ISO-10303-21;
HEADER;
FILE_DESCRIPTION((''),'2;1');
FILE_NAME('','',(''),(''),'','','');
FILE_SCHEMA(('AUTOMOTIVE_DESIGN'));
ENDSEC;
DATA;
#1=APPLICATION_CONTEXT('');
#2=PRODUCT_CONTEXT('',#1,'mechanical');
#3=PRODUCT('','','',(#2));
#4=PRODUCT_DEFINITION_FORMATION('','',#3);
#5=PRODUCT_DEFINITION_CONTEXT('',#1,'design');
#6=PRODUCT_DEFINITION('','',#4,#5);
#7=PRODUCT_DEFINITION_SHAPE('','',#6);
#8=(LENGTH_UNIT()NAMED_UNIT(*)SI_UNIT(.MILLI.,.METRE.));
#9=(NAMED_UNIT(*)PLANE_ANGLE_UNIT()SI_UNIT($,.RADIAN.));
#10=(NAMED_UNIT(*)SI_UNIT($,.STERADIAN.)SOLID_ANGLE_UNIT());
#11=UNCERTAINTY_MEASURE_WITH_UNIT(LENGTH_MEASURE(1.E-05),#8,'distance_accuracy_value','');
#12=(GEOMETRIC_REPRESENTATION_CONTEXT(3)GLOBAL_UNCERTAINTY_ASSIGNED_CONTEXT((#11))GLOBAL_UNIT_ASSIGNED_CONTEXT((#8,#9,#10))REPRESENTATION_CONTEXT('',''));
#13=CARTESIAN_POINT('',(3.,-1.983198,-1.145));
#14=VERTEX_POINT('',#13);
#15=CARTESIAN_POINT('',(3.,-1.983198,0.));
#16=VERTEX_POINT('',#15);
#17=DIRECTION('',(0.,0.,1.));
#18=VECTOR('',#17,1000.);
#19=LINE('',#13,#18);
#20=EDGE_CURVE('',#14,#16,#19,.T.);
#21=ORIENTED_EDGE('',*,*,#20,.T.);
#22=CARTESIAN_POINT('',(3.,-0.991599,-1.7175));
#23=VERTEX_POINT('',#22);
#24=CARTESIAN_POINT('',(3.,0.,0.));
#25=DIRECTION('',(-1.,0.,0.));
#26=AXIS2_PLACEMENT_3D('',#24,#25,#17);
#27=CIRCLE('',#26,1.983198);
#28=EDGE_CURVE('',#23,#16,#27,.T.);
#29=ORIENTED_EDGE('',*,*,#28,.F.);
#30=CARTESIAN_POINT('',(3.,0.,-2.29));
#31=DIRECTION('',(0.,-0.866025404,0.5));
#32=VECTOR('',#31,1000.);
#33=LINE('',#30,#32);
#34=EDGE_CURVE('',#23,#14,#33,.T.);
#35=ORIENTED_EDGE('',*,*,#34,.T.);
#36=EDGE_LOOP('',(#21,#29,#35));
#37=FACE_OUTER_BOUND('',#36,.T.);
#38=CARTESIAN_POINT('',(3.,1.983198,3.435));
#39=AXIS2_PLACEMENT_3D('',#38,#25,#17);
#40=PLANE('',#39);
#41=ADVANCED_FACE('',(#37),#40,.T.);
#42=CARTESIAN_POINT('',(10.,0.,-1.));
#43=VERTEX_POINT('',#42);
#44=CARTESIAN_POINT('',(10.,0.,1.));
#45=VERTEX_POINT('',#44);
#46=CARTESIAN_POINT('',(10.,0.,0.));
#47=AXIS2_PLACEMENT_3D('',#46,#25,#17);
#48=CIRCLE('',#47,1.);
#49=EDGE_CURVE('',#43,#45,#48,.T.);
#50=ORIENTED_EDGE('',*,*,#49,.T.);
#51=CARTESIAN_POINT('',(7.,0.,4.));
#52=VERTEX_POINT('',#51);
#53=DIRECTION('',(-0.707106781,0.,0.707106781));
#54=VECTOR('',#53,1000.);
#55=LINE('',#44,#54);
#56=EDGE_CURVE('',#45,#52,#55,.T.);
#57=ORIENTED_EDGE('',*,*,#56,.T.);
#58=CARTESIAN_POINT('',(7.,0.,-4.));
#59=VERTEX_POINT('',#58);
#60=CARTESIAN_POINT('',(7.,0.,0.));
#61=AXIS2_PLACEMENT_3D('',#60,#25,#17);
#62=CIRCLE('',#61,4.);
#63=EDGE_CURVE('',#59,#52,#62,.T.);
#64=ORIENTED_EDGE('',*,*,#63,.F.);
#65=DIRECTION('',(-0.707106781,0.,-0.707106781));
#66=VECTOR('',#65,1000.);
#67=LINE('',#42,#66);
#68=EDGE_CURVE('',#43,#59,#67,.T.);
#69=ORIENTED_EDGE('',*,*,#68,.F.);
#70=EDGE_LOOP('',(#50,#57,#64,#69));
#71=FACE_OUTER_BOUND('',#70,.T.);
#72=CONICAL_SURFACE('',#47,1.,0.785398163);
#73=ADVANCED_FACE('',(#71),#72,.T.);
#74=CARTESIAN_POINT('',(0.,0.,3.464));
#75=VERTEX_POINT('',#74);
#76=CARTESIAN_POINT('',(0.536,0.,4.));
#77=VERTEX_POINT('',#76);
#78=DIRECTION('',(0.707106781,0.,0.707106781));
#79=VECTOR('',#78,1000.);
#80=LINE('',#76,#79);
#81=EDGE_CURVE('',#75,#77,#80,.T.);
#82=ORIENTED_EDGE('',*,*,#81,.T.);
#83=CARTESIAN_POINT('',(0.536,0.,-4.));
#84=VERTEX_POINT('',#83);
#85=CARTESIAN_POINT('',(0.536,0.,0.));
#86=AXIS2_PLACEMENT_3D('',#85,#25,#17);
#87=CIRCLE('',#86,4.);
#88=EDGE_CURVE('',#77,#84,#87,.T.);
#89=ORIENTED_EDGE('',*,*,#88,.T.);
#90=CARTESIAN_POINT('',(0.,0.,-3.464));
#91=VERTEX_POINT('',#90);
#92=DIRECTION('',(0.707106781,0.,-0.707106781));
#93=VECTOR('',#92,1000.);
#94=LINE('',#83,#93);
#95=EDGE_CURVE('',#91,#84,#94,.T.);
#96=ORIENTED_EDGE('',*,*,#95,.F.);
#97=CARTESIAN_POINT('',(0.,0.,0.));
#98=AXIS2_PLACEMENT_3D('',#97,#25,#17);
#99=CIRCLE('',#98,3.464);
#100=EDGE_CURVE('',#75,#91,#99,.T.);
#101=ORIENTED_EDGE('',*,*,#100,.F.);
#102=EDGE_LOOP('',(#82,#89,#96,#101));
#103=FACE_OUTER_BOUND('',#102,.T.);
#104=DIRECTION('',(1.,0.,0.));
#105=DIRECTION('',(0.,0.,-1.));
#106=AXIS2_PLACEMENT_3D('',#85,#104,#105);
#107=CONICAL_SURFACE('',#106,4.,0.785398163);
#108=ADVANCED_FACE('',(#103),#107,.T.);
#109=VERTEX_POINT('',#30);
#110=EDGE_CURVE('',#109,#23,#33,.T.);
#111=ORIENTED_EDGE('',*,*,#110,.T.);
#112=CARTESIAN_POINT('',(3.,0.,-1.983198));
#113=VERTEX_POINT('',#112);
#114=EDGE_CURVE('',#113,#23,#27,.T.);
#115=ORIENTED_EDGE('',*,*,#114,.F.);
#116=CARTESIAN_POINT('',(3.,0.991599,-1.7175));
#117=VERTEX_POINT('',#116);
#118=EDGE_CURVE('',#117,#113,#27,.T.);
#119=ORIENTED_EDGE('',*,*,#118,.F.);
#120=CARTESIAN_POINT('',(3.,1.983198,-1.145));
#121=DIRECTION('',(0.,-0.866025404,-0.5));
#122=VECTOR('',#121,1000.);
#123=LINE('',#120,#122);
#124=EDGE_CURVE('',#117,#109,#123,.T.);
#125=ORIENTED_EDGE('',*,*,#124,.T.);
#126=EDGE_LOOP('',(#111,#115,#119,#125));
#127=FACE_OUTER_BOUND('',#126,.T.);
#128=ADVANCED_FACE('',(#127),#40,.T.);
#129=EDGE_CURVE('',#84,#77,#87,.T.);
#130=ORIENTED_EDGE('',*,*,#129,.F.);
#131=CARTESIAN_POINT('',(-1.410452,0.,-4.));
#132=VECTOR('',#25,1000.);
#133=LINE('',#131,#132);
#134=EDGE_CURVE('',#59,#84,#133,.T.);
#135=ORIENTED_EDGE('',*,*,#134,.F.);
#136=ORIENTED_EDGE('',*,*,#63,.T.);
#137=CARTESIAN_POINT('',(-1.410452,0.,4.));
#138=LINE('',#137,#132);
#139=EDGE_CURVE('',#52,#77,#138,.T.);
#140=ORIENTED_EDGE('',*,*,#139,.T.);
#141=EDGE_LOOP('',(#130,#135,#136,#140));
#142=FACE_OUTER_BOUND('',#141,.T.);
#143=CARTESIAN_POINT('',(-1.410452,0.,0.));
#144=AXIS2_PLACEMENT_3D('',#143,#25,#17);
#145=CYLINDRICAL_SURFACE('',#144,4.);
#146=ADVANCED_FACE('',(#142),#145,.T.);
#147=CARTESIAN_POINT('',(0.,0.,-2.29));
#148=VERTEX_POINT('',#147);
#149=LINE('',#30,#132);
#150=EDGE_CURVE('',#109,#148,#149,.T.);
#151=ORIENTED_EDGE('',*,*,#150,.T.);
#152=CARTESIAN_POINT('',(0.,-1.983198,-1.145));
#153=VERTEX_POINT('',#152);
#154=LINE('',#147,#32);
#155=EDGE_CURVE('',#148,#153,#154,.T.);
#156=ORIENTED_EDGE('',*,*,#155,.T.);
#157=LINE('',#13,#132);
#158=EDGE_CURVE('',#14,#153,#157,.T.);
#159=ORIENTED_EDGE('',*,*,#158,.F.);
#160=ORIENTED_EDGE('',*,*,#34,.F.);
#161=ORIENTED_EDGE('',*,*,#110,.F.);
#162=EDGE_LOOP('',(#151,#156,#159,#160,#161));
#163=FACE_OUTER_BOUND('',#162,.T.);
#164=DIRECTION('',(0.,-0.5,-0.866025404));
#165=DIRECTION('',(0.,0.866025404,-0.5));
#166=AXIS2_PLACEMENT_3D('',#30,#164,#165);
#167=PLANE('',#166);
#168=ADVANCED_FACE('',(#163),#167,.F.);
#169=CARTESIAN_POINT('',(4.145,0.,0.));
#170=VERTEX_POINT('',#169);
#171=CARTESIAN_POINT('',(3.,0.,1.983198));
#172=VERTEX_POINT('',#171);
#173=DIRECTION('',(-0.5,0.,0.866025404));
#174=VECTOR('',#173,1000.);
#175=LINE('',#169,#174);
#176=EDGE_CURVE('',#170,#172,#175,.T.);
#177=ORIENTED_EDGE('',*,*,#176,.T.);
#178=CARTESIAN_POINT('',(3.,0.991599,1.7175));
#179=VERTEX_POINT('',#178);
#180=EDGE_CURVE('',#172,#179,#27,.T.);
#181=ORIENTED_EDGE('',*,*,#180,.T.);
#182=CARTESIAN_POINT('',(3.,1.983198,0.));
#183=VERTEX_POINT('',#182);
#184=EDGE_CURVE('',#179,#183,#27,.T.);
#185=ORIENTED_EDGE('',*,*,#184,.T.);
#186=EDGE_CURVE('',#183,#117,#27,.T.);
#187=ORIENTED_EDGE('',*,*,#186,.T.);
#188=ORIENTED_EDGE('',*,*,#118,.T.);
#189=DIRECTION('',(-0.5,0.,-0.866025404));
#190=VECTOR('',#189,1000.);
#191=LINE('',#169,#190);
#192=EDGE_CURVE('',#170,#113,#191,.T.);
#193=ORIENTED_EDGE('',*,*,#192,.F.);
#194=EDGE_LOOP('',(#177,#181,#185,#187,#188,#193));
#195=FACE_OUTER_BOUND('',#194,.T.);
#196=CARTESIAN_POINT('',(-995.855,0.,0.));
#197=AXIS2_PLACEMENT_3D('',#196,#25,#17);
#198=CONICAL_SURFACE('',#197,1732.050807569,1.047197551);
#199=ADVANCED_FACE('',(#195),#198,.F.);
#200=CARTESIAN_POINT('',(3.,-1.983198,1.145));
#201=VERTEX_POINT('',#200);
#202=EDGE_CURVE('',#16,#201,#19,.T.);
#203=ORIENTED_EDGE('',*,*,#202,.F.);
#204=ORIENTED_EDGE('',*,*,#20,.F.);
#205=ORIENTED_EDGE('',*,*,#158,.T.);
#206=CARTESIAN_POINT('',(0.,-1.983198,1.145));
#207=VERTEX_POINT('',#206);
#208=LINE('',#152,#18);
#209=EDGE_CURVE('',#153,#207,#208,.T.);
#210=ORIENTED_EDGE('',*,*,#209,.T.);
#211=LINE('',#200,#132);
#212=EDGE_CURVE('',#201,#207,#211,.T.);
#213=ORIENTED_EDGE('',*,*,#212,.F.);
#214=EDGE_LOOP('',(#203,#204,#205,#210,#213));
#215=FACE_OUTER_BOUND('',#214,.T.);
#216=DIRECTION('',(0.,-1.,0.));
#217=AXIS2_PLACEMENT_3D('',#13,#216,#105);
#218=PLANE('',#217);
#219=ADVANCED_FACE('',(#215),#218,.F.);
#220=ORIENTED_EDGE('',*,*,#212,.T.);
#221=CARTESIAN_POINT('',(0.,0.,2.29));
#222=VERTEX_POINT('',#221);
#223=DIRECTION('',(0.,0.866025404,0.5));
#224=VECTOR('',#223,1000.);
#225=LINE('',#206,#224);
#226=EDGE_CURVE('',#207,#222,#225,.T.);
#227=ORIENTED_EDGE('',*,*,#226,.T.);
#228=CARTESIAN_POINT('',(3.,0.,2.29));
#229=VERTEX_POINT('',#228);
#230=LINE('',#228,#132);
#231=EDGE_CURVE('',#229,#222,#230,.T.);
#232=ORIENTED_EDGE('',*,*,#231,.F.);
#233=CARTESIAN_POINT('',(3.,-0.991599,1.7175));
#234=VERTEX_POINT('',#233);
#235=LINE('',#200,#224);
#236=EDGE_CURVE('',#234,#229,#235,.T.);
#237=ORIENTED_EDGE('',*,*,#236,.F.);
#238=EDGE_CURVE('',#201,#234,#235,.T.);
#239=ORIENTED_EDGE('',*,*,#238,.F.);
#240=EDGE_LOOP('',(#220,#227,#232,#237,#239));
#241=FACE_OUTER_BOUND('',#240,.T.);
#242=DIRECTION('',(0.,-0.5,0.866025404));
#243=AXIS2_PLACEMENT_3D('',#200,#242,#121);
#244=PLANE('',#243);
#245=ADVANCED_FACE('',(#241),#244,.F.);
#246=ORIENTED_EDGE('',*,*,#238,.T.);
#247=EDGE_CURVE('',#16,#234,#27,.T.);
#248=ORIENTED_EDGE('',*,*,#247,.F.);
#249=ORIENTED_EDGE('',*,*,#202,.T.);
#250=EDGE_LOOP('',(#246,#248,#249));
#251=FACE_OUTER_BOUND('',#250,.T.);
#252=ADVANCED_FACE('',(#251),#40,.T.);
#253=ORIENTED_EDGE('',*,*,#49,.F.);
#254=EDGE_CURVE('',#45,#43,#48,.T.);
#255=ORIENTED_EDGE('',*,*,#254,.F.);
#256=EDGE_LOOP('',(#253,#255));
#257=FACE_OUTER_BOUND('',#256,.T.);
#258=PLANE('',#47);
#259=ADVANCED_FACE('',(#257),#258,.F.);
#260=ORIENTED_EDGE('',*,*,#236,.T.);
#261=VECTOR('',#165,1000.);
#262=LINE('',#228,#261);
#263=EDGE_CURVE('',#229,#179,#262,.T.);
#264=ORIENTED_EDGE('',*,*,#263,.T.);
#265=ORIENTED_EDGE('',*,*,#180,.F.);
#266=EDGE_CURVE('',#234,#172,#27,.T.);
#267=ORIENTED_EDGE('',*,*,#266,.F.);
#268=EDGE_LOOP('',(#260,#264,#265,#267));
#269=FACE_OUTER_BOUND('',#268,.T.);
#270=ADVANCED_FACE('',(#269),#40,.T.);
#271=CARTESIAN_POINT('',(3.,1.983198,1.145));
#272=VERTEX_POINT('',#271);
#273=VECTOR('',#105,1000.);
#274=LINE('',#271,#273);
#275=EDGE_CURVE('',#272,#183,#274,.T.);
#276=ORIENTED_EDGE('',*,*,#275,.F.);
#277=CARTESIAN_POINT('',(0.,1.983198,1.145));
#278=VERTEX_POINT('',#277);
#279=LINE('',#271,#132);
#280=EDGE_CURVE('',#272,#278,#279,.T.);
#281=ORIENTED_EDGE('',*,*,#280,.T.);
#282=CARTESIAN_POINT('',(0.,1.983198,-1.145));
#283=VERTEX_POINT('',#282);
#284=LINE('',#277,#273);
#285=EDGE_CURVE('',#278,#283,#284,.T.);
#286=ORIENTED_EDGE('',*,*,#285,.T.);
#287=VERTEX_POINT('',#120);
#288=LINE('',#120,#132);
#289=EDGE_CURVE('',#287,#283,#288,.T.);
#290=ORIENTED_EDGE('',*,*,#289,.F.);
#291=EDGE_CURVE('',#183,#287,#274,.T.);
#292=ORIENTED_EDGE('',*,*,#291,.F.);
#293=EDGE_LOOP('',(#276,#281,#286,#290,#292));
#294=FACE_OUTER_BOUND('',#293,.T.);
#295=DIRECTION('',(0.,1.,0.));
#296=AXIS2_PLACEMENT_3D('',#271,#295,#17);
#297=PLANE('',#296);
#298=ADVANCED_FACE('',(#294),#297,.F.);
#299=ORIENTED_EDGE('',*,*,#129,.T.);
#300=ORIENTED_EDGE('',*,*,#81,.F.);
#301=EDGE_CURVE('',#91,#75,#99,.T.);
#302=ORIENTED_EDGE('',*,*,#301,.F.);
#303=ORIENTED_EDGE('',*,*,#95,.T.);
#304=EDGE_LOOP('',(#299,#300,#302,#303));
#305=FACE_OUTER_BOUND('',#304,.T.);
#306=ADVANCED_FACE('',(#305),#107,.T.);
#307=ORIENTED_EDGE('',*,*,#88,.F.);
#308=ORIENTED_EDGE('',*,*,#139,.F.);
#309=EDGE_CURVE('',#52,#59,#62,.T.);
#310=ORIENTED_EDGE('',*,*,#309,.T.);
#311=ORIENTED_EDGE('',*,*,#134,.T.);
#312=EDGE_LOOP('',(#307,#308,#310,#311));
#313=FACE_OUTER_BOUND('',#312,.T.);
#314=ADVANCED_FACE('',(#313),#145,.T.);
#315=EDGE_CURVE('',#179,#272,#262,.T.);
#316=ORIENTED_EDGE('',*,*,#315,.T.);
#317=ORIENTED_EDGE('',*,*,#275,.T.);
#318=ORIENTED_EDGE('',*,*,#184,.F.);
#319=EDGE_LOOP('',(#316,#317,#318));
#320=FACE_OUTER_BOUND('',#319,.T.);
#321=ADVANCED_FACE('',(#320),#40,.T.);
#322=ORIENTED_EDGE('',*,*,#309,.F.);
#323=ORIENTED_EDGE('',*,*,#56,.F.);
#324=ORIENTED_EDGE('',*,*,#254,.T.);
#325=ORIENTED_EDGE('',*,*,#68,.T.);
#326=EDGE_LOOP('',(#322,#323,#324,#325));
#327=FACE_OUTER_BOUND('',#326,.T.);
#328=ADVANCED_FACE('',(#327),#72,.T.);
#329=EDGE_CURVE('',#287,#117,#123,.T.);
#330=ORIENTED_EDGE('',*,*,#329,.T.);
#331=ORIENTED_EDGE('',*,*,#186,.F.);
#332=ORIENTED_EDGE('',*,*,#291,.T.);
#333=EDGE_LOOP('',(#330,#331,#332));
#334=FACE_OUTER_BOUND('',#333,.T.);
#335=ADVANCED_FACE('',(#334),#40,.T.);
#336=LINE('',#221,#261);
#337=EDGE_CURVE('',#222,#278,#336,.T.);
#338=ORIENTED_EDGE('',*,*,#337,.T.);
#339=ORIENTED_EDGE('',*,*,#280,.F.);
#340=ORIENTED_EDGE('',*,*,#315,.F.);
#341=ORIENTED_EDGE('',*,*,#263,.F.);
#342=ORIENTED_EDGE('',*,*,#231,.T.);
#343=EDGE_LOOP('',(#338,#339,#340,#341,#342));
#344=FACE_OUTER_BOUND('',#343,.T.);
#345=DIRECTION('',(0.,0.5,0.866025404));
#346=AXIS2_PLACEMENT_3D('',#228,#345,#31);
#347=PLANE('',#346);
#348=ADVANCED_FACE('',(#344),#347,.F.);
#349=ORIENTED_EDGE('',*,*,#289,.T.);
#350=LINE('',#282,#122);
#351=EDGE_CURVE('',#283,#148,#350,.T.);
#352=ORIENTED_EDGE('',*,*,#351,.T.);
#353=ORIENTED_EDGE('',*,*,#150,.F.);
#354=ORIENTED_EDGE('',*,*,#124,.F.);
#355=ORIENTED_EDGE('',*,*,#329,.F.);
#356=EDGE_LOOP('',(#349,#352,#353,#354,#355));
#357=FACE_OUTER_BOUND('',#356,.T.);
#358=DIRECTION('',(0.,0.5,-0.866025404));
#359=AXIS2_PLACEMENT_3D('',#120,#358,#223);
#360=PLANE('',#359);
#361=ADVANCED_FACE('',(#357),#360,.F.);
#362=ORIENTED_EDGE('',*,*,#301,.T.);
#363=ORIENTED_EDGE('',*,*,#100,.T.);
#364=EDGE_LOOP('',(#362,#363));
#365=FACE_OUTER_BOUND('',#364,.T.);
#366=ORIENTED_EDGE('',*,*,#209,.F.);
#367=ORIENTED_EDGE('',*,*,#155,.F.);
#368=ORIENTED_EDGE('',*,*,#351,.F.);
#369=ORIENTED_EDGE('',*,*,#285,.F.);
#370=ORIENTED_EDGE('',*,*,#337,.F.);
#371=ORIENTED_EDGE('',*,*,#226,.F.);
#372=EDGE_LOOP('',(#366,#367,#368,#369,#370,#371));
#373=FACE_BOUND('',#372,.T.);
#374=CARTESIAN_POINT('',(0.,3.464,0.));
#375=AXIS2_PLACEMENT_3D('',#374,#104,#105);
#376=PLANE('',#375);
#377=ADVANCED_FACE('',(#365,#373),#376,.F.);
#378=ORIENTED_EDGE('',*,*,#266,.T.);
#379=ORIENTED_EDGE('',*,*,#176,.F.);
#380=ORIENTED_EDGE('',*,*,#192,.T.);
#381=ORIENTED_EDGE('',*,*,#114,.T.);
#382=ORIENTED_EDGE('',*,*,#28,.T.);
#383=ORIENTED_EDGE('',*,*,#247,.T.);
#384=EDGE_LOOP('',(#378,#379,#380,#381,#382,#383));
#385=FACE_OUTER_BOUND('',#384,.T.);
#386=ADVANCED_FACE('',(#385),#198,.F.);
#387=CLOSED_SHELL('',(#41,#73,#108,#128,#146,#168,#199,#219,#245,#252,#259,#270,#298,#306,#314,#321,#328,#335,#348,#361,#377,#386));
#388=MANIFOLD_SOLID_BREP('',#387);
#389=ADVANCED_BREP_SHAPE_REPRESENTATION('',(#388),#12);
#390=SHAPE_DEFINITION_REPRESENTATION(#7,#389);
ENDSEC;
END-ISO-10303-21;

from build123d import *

# Parameters (mm, degrees)
CUT_EXTRUDE_1_DEPTH = 3


with BuildPart() as part:
    # 草图1 → Revolve 552 (revolve)
    with BuildSketch(Plane.XY, mode=Mode.PRIVATE) as revolve_552_sk:
        Polygon((0, 0), (10, 0), (10, 1), (7, 4), (0.536, 4), (0, 3.464), align=None)
    revolve(revolve_552_sk.sketch.rotate(Axis((-1.4104518, 0, 0), (1, 0, 0)), 90), axis=Axis((-1.4104518, 0, 0), (1, 0, 0)))

    # 草图2 → 切除-拉伸1 (cut)
    with BuildSketch(Plane.ZY):
        Polygon((2.29, 0), (1.145, 1.983198175), (-1.145, 1.983198175), (-2.29, 0), (-1.145, -1.983198175), (1.145, -1.983198175), align=None)
    extrude(amount=-CUT_EXTRUDE_1_DEPTH, mode=Mode.SUBTRACT)

    # 草图3 → 切除-旋转1 (revolve, cut)
    with BuildSketch(Plane.XY, mode=Mode.PRIVATE) as cut_revolve_1_sk:
        Polygon((3, 1.983198175), (4.145, 0), (3, 0), align=None)
    revolve(cut_revolve_1_sk.sketch.rotate(Axis((-0.121283255, 0, 0), (1, 0, 0)), 90), axis=Axis((-0.121283255, 0, 0), (1, 0, 0)), mode=Mode.SUBTRACT)


solid = part.part
